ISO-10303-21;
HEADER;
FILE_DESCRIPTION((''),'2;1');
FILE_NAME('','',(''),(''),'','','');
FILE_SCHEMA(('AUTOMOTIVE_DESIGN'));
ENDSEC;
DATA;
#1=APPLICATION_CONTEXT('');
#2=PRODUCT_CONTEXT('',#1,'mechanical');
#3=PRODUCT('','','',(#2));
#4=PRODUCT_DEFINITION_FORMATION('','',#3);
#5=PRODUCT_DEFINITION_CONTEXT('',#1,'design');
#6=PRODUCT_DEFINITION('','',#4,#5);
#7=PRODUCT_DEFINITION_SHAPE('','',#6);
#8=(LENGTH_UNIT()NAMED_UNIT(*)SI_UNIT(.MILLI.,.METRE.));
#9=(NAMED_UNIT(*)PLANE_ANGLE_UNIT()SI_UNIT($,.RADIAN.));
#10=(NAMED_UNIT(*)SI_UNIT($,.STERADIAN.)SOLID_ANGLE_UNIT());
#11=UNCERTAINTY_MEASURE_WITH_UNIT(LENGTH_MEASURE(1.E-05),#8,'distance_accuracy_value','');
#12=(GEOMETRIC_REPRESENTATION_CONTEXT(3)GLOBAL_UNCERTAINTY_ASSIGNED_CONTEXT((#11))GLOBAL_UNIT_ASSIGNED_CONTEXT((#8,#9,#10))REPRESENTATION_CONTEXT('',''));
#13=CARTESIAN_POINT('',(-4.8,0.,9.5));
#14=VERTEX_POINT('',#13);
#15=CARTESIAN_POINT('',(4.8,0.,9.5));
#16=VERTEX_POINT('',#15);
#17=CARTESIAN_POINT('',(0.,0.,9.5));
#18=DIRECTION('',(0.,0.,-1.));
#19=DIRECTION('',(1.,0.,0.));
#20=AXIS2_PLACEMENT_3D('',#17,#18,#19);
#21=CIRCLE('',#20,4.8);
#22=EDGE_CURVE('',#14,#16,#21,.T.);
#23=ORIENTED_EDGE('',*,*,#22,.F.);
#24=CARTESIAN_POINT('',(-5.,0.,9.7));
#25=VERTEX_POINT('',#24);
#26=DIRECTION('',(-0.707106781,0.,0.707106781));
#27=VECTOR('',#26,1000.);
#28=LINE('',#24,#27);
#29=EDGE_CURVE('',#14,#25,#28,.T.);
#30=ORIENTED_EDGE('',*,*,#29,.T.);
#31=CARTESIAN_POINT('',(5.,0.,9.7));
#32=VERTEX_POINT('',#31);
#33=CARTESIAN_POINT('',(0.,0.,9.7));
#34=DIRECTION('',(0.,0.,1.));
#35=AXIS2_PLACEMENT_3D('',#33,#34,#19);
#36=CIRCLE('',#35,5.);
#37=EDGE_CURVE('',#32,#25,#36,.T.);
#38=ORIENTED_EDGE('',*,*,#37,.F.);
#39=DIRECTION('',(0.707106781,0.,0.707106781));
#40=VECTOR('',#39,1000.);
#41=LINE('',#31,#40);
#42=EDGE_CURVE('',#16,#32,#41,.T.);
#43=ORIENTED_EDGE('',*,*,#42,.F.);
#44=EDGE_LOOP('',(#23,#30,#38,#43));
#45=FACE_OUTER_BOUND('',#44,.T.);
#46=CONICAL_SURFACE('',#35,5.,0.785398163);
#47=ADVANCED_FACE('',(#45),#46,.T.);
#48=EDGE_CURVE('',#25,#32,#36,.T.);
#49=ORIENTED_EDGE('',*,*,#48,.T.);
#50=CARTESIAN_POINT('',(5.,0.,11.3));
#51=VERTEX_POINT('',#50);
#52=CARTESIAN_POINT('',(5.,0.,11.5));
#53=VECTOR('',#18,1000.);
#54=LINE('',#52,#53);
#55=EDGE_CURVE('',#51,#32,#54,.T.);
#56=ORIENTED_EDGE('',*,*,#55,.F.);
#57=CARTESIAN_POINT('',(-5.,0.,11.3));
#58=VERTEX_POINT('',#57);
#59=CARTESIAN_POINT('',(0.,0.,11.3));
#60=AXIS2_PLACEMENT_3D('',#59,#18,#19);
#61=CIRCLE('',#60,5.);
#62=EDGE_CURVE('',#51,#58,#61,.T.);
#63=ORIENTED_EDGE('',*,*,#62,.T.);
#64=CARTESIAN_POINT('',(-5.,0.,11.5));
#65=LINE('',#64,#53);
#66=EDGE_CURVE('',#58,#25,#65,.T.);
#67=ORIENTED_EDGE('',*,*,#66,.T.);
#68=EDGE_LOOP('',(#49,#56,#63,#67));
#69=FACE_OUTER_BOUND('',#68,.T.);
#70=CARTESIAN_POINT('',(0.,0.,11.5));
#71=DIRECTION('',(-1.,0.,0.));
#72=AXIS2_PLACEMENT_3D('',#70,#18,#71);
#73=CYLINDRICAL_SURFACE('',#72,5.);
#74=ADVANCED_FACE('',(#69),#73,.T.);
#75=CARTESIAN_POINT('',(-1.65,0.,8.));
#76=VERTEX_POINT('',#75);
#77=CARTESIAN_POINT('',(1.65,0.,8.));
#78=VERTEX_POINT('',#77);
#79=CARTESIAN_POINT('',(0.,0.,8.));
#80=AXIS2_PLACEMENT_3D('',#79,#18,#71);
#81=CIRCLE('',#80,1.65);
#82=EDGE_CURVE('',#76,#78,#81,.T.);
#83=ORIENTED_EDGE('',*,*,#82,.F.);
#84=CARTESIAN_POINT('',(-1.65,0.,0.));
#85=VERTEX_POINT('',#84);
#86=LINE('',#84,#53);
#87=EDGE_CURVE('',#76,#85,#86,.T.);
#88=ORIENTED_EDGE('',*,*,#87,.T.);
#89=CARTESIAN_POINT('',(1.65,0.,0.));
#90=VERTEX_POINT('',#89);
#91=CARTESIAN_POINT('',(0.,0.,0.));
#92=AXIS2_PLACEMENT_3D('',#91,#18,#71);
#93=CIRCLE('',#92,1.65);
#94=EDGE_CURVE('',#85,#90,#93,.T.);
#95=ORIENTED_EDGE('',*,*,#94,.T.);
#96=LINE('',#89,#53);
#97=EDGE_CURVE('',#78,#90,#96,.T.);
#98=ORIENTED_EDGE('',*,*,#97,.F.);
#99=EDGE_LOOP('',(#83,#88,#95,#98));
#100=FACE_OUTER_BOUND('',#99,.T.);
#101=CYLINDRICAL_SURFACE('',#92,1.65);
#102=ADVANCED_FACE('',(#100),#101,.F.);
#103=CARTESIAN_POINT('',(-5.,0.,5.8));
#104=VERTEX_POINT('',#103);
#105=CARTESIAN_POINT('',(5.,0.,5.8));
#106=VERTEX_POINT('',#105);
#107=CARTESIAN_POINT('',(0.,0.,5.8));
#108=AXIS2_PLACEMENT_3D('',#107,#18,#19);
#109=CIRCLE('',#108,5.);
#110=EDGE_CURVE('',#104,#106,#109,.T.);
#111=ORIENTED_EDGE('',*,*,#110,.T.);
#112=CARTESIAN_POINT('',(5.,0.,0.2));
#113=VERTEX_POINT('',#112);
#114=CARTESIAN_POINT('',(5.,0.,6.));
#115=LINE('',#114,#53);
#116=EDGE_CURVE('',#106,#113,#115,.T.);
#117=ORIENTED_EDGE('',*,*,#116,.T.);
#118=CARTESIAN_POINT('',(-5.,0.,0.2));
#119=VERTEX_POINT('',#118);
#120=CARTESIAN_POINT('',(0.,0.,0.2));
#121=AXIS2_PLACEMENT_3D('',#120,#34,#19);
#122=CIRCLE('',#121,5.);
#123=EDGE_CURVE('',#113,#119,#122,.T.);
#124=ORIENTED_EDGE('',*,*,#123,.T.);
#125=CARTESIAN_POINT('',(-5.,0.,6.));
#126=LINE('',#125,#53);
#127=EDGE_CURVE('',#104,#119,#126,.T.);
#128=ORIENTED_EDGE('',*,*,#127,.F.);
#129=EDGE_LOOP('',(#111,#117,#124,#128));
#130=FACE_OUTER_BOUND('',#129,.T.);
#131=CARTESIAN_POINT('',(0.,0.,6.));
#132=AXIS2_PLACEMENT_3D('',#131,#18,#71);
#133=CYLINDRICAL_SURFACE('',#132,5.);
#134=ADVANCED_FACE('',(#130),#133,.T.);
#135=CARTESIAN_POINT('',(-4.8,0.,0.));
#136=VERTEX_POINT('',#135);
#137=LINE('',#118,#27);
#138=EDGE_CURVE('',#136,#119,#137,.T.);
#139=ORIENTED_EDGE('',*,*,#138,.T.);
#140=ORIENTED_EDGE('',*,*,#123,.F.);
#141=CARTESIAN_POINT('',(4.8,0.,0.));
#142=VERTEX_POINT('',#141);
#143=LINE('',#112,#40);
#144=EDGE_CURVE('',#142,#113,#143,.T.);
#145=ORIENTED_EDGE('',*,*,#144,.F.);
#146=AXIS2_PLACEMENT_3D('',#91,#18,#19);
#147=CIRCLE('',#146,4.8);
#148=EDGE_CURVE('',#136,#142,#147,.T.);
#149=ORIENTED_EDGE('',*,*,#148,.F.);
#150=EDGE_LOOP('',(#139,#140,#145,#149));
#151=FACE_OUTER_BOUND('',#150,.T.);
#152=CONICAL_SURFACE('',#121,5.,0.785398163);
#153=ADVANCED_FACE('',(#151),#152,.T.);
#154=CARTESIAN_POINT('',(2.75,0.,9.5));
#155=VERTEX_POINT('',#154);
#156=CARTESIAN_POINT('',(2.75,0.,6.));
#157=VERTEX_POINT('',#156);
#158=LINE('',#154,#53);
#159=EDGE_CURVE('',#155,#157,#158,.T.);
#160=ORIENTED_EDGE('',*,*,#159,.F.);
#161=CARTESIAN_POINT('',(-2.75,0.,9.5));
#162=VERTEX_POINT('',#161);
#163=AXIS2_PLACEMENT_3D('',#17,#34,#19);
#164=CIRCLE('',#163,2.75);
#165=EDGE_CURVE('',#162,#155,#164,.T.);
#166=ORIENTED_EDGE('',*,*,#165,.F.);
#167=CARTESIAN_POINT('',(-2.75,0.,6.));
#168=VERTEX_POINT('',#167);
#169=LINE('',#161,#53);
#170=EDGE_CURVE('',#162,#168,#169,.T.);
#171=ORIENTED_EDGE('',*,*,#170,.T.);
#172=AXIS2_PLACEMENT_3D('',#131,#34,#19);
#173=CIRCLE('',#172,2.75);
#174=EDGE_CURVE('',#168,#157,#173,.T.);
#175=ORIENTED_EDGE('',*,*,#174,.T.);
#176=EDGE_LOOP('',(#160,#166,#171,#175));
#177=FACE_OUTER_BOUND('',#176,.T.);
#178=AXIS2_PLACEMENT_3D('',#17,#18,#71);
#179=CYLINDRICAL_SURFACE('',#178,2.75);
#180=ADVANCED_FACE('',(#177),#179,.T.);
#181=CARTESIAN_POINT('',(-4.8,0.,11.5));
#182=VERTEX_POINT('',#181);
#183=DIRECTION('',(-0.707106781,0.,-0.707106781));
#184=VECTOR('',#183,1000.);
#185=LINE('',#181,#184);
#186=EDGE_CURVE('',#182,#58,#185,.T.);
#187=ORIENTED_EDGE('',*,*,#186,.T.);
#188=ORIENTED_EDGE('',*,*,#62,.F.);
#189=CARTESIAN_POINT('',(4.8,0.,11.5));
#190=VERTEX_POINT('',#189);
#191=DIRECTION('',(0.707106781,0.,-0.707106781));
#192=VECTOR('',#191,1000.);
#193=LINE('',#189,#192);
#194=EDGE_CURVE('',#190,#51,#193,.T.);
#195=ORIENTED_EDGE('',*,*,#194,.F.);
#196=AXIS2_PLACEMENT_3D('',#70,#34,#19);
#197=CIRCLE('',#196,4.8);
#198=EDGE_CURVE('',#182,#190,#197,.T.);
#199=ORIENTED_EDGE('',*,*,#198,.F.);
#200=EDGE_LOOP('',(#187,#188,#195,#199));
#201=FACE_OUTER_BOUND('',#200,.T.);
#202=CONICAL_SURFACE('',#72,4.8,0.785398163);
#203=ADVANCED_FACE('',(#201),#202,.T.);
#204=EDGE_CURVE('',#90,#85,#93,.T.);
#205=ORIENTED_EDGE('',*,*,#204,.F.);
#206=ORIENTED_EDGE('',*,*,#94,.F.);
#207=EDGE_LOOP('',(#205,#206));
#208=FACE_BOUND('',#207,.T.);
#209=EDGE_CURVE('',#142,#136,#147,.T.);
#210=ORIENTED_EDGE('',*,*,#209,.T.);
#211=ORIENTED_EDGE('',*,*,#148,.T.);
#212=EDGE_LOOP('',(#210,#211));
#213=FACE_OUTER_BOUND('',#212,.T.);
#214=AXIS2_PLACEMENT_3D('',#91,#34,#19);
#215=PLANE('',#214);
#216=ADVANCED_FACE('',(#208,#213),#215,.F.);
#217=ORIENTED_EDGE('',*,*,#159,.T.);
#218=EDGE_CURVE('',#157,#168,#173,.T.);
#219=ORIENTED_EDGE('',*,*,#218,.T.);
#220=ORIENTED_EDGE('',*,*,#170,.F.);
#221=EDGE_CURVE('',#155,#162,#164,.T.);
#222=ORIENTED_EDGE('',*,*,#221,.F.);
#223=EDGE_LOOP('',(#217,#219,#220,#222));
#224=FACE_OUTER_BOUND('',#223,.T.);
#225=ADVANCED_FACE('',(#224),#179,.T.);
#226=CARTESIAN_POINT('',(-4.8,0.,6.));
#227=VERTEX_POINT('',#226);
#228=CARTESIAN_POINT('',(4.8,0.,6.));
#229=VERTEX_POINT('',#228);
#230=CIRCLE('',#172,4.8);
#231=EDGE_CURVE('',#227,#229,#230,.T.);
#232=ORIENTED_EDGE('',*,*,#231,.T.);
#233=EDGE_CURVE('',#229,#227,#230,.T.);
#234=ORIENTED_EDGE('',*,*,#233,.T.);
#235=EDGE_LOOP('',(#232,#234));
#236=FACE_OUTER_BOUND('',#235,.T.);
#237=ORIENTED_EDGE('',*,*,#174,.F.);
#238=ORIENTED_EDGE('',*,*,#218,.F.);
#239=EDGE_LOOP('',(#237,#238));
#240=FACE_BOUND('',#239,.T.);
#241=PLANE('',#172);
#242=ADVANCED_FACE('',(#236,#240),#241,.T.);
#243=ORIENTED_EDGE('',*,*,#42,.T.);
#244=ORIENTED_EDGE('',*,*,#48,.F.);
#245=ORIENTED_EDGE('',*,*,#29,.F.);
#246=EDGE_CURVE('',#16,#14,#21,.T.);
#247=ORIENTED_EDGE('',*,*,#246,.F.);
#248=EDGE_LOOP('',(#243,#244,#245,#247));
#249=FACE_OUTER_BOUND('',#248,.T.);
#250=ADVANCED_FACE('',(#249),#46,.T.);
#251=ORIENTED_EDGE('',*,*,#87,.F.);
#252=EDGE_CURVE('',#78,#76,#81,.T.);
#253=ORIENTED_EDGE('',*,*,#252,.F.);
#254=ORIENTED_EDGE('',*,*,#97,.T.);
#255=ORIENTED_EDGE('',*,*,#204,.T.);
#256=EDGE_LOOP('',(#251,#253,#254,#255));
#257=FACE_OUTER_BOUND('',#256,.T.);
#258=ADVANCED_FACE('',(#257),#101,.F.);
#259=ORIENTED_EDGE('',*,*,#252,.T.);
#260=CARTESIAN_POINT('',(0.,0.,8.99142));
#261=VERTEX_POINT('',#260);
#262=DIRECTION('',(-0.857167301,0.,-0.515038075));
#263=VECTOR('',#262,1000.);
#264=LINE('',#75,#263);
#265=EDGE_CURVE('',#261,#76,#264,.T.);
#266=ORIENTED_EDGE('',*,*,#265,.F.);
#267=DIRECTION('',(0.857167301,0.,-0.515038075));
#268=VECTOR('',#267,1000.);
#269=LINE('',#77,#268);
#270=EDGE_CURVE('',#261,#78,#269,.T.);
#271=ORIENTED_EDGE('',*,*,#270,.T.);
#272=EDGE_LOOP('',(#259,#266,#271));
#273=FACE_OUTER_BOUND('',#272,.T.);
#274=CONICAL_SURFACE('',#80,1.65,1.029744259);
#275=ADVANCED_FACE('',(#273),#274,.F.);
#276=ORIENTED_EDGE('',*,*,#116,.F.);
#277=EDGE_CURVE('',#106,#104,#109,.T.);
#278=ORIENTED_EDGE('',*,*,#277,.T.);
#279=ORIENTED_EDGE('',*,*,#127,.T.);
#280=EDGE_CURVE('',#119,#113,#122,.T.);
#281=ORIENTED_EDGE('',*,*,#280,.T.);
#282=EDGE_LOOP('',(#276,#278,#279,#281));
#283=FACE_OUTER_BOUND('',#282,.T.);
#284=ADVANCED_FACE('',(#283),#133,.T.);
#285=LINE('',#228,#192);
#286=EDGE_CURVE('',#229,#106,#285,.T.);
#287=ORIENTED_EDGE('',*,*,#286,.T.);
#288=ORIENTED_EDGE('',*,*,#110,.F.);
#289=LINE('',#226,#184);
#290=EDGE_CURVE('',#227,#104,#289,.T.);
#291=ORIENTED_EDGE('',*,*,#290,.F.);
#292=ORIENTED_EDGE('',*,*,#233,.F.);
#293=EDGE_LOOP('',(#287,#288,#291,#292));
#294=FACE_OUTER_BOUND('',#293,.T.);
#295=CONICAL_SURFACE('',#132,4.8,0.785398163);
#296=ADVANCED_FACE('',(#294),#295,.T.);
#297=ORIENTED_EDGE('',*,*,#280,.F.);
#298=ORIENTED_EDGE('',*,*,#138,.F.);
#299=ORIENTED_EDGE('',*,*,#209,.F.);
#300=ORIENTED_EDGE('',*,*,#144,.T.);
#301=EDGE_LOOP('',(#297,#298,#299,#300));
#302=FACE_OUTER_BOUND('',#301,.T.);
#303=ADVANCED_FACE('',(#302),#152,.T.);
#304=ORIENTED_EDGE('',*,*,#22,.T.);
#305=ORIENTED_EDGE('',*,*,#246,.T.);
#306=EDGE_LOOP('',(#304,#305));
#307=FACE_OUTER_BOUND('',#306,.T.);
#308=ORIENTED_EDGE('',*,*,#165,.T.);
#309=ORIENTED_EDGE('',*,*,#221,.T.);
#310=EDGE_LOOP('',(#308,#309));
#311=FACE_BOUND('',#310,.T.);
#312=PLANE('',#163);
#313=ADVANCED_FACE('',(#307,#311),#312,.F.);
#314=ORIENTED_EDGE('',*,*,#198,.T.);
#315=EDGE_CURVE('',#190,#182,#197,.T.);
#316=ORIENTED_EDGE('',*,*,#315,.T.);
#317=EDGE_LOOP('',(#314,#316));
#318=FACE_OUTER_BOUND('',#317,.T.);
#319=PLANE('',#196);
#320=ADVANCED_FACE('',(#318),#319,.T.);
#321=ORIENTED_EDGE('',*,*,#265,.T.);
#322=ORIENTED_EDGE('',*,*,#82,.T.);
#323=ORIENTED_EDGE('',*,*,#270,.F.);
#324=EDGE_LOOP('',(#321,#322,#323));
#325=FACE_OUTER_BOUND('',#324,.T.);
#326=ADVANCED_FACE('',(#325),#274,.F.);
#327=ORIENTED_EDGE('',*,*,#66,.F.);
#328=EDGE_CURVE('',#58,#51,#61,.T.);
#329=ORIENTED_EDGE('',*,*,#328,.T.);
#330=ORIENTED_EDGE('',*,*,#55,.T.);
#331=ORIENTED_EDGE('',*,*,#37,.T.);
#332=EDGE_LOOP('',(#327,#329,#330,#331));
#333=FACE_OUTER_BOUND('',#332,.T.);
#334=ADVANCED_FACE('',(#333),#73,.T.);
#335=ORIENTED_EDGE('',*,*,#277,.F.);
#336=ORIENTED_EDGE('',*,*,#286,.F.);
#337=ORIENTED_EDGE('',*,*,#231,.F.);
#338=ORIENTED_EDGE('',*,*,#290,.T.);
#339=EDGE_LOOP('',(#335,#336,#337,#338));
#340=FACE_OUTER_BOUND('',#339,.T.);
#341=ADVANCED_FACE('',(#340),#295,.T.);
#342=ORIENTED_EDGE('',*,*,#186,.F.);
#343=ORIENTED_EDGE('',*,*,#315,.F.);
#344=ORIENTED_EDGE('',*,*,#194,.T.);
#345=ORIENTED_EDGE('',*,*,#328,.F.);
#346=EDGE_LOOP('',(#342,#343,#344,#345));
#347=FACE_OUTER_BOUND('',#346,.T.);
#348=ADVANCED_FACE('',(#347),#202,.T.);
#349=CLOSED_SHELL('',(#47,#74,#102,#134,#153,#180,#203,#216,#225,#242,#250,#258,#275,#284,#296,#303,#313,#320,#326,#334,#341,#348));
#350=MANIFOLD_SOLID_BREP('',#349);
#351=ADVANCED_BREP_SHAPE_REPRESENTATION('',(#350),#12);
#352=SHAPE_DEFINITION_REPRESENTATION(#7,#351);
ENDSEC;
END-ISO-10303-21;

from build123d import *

# Parameters (mm, degrees)
SKETCH1_R             = 5
BOSS_EXTRUDE1_DEPTH   = 6
SKETCH2_R             = 2.75
BOSS_EXTRUDE2_DEPTH   = 3.5
SKETCH3_R             = 5
BOSS_EXTRUDE3_DEPTH   = 2
M4_TAPPED_HOLE1_D     = 3.3
M4_TAPPED_HOLE1_DEPTH = 8
M4_TAPPED_HOLE1_TIP   = 0.991420021
CHAMFER1_SIZE         = 0.2


with BuildPart() as part:
    # Sketch1 → Boss-Extrude1 (new body)
    with BuildSketch(Plane.XY):
        Circle(SKETCH1_R)
    extrude(amount=BOSS_EXTRUDE1_DEPTH)

    # Sketch2 → Boss-Extrude2 (add)
    with BuildSketch(Plane.XY.offset(6)):
        Circle(SKETCH2_R)
    extrude(amount=BOSS_EXTRUDE2_DEPTH)

    # Sketch3 → Boss-Extrude3 (add)
    with BuildSketch(Plane.XY.offset(9.5)):
        Circle(SKETCH3_R)
    extrude(amount=BOSS_EXTRUDE3_DEPTH)

    # M4 tapped hole1
    with Locations(Plane(origin=(0, 0, 0), x_dir=(-1, 0, 0), z_dir=(0, 0, -1))):
        with Locations((0, 0)):
            Hole(M4_TAPPED_HOLE1_D / 2, depth=M4_TAPPED_HOLE1_DEPTH)
            with Locations((0, 0, -(M4_TAPPED_HOLE1_DEPTH + M4_TAPPED_HOLE1_TIP / 2))):  # 118° drill point
                Cone(0, M4_TAPPED_HOLE1_D / 2, M4_TAPPED_HOLE1_TIP, mode=Mode.SUBTRACT)

    # Chamfer1
    chamfer1_edges = [part.edges().sort_by_distance(p)[0] for p in [
        (-5, 0, 0),
        (-5, 0, 6),
        (-5, 0, 9.5),
        (-5, 0, 11.5),
    ]]
    chamfer(chamfer1_edges, length=CHAMFER1_SIZE)


solid = part.part
